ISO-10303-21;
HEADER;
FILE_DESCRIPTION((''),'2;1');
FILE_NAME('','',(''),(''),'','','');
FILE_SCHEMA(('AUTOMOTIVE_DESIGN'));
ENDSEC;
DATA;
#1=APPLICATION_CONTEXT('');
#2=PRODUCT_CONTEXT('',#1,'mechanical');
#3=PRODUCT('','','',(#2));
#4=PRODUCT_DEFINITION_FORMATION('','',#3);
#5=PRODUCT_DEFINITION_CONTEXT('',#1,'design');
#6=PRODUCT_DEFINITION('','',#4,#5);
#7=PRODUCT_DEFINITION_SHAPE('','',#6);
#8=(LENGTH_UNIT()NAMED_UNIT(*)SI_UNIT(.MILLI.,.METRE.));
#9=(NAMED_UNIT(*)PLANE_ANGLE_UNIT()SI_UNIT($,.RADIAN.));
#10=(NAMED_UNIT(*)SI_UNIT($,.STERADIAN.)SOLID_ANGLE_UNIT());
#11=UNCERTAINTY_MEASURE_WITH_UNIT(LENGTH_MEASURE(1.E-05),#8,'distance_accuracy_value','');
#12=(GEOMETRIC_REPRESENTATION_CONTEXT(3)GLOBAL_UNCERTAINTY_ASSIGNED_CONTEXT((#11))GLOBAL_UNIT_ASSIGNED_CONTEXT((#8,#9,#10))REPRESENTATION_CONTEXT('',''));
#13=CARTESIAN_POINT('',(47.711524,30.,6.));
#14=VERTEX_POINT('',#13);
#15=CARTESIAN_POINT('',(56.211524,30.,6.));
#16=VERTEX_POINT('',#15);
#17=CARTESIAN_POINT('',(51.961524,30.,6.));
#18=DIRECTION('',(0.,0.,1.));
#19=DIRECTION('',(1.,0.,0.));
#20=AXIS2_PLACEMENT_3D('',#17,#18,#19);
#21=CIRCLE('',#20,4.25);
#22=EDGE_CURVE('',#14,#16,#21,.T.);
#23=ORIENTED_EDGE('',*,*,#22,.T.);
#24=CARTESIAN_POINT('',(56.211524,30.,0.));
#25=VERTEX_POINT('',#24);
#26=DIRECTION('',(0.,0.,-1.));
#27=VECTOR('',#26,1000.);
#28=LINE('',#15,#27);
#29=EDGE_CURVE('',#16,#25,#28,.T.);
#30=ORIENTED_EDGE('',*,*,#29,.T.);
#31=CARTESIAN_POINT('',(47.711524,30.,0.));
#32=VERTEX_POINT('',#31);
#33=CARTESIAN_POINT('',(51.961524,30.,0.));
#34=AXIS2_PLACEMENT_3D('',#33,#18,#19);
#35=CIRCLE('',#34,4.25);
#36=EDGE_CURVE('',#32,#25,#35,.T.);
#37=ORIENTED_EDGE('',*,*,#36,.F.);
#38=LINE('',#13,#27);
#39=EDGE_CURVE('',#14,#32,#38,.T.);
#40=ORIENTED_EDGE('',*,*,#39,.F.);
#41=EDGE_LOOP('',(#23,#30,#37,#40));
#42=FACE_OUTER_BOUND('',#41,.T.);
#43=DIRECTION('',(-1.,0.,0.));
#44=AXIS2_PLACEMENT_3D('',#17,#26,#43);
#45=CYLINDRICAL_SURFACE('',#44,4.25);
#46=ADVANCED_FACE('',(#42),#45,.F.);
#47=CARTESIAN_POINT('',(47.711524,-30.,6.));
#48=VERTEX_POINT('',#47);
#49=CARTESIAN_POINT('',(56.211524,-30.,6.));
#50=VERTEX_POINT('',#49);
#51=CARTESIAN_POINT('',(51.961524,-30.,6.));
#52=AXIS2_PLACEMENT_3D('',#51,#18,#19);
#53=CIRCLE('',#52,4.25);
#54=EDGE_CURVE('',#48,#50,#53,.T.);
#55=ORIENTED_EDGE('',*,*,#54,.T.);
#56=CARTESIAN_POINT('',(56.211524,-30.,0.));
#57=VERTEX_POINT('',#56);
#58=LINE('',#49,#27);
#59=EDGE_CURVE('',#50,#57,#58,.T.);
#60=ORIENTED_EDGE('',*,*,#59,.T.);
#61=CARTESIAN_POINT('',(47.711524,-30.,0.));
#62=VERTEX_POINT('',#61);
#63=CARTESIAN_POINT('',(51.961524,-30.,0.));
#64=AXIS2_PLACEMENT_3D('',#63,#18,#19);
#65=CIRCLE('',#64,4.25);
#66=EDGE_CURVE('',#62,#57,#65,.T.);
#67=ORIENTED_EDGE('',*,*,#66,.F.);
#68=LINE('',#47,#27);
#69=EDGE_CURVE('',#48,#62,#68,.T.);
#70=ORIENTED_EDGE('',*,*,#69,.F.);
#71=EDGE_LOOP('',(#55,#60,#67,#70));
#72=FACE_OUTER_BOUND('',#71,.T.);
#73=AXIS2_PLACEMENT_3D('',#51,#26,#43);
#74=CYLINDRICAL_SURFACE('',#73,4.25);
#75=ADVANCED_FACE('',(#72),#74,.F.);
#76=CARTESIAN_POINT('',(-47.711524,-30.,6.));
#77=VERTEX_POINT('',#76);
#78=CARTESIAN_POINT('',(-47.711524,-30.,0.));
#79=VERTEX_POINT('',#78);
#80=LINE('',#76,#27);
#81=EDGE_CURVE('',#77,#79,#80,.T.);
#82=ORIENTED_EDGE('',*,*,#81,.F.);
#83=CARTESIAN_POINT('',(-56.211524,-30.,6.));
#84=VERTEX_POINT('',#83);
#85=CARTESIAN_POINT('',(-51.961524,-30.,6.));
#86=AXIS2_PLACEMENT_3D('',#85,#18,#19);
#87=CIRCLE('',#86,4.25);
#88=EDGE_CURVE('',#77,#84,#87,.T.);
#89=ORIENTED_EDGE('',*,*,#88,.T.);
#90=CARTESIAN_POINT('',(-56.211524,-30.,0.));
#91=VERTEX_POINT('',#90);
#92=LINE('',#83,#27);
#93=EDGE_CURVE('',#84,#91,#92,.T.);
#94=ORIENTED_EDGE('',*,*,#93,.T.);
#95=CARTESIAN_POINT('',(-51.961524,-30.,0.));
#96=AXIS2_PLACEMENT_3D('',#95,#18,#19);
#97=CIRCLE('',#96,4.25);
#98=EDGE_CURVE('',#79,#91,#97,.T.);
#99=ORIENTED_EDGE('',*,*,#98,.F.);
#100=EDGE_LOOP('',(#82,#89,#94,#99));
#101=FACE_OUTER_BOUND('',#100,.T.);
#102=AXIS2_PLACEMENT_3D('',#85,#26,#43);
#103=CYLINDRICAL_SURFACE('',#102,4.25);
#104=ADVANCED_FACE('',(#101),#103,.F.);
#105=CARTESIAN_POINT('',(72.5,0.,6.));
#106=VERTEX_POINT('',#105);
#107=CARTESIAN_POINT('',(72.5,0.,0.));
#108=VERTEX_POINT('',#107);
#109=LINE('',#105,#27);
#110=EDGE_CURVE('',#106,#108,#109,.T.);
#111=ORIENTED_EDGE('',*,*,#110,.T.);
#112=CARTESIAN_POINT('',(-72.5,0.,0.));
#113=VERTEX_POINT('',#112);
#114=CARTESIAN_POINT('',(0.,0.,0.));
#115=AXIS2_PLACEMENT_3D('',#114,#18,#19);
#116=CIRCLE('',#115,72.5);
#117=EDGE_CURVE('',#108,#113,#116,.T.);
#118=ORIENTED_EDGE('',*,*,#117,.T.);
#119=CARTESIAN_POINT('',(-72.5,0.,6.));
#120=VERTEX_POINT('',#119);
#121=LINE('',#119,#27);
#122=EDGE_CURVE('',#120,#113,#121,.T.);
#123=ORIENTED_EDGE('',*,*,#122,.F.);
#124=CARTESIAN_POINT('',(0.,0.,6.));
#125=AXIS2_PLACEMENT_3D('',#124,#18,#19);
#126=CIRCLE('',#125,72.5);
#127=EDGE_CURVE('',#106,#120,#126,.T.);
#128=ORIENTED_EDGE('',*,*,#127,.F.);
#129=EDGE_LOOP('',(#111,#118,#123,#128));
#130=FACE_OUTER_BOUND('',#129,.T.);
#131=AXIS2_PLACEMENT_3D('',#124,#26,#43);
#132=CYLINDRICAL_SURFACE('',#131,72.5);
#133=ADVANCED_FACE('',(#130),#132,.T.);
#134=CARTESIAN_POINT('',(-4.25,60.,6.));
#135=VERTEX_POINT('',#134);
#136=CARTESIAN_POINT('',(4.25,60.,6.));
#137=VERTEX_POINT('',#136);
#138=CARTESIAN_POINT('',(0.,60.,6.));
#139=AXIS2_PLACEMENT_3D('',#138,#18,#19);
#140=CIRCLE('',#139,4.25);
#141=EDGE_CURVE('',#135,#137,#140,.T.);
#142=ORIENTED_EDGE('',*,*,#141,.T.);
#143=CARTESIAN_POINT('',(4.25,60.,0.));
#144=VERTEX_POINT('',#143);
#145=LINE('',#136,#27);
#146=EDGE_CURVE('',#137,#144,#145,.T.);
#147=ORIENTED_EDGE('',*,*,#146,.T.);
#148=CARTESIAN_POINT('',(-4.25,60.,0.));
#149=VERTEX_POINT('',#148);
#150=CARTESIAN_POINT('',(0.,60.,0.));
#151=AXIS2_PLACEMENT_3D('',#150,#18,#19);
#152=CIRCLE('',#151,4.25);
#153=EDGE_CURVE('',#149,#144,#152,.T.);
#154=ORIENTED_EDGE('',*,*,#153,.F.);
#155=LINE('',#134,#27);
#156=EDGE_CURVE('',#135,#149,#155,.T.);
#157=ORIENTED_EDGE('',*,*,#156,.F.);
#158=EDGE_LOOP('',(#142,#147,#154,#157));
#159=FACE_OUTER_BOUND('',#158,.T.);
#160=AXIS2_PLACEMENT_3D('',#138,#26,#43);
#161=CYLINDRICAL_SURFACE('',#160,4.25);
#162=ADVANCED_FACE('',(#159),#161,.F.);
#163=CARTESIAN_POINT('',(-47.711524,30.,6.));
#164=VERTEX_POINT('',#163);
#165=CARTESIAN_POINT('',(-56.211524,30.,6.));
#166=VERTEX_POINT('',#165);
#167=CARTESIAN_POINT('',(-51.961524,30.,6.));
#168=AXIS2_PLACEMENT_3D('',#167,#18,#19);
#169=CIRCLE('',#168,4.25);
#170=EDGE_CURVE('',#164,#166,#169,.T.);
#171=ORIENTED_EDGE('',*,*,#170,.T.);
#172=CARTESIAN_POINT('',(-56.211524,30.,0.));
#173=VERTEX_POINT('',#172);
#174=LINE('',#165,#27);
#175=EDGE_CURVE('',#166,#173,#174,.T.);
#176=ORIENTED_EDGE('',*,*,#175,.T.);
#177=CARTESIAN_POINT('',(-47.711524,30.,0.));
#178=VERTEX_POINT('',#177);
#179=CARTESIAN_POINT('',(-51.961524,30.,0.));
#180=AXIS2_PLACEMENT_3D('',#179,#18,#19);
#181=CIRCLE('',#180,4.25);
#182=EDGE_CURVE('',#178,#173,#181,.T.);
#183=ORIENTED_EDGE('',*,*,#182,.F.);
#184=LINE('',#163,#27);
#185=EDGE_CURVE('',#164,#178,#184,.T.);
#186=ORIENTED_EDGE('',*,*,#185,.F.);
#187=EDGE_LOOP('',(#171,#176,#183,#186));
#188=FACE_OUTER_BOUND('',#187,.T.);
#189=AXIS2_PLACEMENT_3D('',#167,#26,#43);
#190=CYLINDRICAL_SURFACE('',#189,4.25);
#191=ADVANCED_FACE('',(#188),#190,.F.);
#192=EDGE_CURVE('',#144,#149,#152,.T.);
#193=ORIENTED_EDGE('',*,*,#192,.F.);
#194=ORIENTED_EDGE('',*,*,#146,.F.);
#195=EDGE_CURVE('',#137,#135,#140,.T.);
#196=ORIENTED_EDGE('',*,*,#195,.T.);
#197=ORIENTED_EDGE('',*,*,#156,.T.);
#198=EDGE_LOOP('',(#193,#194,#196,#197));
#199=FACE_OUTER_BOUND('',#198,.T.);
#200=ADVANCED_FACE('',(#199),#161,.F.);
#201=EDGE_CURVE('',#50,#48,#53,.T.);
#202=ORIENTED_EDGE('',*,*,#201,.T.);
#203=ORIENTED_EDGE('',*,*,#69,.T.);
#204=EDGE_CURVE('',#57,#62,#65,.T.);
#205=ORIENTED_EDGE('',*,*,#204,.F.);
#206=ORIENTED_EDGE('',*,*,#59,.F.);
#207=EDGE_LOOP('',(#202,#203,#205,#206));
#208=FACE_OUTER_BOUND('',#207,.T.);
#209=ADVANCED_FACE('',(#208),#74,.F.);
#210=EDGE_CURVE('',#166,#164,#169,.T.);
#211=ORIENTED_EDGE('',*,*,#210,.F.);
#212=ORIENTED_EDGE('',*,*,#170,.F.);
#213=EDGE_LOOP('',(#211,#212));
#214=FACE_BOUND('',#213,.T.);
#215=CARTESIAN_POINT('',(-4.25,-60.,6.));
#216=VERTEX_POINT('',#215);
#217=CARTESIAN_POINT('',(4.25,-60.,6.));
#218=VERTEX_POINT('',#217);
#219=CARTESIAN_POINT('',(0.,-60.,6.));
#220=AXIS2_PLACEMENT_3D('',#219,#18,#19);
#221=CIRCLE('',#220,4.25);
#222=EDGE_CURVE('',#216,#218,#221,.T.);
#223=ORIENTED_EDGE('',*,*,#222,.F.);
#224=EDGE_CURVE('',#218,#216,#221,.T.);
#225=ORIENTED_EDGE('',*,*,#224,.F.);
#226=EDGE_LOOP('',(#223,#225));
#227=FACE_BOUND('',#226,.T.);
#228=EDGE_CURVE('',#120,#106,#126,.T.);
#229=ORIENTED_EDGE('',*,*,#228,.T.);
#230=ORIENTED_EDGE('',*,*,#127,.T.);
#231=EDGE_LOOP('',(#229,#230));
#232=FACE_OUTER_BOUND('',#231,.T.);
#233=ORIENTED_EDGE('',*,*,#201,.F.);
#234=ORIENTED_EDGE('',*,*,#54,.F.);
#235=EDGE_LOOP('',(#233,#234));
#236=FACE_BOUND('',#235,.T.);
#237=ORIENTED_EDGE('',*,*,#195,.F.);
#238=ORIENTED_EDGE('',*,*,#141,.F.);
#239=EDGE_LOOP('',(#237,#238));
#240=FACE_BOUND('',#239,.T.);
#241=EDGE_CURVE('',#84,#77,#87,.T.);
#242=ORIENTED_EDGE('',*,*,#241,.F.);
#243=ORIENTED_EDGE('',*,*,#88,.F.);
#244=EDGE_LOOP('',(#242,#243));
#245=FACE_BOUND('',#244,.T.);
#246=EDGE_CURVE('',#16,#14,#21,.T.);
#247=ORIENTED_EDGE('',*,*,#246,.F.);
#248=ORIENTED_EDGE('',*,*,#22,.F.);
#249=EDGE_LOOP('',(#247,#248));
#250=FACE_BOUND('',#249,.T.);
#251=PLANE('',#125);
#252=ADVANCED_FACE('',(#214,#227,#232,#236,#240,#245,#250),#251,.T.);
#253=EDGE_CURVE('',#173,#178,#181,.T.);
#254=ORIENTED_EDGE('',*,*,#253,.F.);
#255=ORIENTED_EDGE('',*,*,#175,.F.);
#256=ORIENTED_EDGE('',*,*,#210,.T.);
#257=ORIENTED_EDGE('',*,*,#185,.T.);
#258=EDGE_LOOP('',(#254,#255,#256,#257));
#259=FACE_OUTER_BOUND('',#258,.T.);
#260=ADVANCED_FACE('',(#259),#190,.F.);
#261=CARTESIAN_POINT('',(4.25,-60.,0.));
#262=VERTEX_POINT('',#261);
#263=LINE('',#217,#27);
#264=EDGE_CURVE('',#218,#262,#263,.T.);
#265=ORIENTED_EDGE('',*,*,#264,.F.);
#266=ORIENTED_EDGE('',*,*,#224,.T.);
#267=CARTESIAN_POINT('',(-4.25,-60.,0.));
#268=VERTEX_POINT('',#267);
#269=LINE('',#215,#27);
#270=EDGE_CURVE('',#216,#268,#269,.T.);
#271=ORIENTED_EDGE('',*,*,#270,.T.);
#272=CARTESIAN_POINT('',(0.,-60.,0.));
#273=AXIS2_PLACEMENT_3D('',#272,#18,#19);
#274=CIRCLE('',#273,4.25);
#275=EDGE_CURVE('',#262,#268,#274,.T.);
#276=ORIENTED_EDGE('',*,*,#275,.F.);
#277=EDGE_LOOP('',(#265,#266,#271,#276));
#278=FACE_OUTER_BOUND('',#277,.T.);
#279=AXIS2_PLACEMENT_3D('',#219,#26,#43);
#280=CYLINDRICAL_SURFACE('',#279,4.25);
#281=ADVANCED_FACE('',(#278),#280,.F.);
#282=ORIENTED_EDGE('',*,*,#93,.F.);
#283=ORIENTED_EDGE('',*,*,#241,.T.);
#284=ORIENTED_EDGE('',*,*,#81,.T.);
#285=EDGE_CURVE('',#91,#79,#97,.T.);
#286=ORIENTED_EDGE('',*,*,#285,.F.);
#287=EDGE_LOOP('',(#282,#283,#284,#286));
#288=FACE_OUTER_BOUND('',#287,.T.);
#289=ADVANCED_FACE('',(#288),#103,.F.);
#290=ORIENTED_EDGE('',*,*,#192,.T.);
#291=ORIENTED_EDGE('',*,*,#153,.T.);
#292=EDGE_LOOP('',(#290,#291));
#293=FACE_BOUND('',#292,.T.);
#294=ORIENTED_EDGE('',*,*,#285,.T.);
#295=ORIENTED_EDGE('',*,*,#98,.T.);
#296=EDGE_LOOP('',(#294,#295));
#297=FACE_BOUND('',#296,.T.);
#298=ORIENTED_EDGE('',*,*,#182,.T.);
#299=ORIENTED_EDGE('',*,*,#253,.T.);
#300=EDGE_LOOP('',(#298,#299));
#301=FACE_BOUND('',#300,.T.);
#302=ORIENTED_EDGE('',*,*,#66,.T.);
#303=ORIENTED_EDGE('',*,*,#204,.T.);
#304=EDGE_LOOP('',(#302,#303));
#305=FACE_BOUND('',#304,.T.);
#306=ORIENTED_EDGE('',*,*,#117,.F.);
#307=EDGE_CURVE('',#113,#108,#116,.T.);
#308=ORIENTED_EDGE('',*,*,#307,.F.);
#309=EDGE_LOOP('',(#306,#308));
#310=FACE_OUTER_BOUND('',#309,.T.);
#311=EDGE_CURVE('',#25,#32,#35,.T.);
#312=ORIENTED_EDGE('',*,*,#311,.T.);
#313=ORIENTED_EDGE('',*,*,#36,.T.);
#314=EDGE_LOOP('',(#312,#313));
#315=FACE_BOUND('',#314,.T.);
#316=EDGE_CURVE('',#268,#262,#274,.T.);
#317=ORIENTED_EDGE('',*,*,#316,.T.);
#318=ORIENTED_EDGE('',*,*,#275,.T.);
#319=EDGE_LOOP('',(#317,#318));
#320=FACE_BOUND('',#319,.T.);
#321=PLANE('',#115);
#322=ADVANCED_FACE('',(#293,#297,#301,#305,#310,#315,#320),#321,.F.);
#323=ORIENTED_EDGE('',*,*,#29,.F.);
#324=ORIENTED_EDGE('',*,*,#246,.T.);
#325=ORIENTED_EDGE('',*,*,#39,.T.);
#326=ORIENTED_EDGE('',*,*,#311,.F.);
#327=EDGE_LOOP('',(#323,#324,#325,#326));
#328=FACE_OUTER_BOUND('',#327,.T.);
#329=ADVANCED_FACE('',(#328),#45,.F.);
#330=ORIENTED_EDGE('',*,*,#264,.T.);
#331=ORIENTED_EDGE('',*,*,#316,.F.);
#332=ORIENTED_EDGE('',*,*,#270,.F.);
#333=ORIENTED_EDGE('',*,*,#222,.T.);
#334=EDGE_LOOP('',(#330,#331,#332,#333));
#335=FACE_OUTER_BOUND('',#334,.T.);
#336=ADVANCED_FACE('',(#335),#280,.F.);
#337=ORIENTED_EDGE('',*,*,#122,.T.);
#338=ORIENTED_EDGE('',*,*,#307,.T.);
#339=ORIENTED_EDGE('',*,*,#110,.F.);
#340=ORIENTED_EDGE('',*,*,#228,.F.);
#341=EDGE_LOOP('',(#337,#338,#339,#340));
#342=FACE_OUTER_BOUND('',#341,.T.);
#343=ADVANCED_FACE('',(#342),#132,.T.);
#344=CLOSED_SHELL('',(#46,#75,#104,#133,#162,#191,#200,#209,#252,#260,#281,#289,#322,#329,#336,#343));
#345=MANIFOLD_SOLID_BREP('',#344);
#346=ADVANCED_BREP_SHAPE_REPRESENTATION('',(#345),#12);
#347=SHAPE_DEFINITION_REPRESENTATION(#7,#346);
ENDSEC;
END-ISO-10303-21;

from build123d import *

# Parameters (mm, degrees)
SKETCH1_R           = 72.5
SKETCH1_R_2         = 4.25
BOSS_EXTRUDE1_DEPTH = 6


with BuildPart() as part:
    # Sketch1 → Boss-Extrude1 (new body)
    with BuildSketch(Plane.XY):
        Circle(SKETCH1_R)
        with Locations((0, 60)):
            Circle(SKETCH1_R_2, mode=Mode.SUBTRACT)
        with Locations((51.961524227, 30)):
            Circle(SKETCH1_R_2, mode=Mode.SUBTRACT)
        with Locations((51.961524227, -30)):
            Circle(SKETCH1_R_2, mode=Mode.SUBTRACT)
        with Locations((0, -60)):
            Circle(SKETCH1_R_2, mode=Mode.SUBTRACT)
        with Locations((-51.961524227, -30)):
            Circle(SKETCH1_R_2, mode=Mode.SUBTRACT)
        with Locations((-51.961524227, 30)):
            Circle(SKETCH1_R_2, mode=Mode.SUBTRACT)
    extrude(amount=BOSS_EXTRUDE1_DEPTH)


solid = part.part
